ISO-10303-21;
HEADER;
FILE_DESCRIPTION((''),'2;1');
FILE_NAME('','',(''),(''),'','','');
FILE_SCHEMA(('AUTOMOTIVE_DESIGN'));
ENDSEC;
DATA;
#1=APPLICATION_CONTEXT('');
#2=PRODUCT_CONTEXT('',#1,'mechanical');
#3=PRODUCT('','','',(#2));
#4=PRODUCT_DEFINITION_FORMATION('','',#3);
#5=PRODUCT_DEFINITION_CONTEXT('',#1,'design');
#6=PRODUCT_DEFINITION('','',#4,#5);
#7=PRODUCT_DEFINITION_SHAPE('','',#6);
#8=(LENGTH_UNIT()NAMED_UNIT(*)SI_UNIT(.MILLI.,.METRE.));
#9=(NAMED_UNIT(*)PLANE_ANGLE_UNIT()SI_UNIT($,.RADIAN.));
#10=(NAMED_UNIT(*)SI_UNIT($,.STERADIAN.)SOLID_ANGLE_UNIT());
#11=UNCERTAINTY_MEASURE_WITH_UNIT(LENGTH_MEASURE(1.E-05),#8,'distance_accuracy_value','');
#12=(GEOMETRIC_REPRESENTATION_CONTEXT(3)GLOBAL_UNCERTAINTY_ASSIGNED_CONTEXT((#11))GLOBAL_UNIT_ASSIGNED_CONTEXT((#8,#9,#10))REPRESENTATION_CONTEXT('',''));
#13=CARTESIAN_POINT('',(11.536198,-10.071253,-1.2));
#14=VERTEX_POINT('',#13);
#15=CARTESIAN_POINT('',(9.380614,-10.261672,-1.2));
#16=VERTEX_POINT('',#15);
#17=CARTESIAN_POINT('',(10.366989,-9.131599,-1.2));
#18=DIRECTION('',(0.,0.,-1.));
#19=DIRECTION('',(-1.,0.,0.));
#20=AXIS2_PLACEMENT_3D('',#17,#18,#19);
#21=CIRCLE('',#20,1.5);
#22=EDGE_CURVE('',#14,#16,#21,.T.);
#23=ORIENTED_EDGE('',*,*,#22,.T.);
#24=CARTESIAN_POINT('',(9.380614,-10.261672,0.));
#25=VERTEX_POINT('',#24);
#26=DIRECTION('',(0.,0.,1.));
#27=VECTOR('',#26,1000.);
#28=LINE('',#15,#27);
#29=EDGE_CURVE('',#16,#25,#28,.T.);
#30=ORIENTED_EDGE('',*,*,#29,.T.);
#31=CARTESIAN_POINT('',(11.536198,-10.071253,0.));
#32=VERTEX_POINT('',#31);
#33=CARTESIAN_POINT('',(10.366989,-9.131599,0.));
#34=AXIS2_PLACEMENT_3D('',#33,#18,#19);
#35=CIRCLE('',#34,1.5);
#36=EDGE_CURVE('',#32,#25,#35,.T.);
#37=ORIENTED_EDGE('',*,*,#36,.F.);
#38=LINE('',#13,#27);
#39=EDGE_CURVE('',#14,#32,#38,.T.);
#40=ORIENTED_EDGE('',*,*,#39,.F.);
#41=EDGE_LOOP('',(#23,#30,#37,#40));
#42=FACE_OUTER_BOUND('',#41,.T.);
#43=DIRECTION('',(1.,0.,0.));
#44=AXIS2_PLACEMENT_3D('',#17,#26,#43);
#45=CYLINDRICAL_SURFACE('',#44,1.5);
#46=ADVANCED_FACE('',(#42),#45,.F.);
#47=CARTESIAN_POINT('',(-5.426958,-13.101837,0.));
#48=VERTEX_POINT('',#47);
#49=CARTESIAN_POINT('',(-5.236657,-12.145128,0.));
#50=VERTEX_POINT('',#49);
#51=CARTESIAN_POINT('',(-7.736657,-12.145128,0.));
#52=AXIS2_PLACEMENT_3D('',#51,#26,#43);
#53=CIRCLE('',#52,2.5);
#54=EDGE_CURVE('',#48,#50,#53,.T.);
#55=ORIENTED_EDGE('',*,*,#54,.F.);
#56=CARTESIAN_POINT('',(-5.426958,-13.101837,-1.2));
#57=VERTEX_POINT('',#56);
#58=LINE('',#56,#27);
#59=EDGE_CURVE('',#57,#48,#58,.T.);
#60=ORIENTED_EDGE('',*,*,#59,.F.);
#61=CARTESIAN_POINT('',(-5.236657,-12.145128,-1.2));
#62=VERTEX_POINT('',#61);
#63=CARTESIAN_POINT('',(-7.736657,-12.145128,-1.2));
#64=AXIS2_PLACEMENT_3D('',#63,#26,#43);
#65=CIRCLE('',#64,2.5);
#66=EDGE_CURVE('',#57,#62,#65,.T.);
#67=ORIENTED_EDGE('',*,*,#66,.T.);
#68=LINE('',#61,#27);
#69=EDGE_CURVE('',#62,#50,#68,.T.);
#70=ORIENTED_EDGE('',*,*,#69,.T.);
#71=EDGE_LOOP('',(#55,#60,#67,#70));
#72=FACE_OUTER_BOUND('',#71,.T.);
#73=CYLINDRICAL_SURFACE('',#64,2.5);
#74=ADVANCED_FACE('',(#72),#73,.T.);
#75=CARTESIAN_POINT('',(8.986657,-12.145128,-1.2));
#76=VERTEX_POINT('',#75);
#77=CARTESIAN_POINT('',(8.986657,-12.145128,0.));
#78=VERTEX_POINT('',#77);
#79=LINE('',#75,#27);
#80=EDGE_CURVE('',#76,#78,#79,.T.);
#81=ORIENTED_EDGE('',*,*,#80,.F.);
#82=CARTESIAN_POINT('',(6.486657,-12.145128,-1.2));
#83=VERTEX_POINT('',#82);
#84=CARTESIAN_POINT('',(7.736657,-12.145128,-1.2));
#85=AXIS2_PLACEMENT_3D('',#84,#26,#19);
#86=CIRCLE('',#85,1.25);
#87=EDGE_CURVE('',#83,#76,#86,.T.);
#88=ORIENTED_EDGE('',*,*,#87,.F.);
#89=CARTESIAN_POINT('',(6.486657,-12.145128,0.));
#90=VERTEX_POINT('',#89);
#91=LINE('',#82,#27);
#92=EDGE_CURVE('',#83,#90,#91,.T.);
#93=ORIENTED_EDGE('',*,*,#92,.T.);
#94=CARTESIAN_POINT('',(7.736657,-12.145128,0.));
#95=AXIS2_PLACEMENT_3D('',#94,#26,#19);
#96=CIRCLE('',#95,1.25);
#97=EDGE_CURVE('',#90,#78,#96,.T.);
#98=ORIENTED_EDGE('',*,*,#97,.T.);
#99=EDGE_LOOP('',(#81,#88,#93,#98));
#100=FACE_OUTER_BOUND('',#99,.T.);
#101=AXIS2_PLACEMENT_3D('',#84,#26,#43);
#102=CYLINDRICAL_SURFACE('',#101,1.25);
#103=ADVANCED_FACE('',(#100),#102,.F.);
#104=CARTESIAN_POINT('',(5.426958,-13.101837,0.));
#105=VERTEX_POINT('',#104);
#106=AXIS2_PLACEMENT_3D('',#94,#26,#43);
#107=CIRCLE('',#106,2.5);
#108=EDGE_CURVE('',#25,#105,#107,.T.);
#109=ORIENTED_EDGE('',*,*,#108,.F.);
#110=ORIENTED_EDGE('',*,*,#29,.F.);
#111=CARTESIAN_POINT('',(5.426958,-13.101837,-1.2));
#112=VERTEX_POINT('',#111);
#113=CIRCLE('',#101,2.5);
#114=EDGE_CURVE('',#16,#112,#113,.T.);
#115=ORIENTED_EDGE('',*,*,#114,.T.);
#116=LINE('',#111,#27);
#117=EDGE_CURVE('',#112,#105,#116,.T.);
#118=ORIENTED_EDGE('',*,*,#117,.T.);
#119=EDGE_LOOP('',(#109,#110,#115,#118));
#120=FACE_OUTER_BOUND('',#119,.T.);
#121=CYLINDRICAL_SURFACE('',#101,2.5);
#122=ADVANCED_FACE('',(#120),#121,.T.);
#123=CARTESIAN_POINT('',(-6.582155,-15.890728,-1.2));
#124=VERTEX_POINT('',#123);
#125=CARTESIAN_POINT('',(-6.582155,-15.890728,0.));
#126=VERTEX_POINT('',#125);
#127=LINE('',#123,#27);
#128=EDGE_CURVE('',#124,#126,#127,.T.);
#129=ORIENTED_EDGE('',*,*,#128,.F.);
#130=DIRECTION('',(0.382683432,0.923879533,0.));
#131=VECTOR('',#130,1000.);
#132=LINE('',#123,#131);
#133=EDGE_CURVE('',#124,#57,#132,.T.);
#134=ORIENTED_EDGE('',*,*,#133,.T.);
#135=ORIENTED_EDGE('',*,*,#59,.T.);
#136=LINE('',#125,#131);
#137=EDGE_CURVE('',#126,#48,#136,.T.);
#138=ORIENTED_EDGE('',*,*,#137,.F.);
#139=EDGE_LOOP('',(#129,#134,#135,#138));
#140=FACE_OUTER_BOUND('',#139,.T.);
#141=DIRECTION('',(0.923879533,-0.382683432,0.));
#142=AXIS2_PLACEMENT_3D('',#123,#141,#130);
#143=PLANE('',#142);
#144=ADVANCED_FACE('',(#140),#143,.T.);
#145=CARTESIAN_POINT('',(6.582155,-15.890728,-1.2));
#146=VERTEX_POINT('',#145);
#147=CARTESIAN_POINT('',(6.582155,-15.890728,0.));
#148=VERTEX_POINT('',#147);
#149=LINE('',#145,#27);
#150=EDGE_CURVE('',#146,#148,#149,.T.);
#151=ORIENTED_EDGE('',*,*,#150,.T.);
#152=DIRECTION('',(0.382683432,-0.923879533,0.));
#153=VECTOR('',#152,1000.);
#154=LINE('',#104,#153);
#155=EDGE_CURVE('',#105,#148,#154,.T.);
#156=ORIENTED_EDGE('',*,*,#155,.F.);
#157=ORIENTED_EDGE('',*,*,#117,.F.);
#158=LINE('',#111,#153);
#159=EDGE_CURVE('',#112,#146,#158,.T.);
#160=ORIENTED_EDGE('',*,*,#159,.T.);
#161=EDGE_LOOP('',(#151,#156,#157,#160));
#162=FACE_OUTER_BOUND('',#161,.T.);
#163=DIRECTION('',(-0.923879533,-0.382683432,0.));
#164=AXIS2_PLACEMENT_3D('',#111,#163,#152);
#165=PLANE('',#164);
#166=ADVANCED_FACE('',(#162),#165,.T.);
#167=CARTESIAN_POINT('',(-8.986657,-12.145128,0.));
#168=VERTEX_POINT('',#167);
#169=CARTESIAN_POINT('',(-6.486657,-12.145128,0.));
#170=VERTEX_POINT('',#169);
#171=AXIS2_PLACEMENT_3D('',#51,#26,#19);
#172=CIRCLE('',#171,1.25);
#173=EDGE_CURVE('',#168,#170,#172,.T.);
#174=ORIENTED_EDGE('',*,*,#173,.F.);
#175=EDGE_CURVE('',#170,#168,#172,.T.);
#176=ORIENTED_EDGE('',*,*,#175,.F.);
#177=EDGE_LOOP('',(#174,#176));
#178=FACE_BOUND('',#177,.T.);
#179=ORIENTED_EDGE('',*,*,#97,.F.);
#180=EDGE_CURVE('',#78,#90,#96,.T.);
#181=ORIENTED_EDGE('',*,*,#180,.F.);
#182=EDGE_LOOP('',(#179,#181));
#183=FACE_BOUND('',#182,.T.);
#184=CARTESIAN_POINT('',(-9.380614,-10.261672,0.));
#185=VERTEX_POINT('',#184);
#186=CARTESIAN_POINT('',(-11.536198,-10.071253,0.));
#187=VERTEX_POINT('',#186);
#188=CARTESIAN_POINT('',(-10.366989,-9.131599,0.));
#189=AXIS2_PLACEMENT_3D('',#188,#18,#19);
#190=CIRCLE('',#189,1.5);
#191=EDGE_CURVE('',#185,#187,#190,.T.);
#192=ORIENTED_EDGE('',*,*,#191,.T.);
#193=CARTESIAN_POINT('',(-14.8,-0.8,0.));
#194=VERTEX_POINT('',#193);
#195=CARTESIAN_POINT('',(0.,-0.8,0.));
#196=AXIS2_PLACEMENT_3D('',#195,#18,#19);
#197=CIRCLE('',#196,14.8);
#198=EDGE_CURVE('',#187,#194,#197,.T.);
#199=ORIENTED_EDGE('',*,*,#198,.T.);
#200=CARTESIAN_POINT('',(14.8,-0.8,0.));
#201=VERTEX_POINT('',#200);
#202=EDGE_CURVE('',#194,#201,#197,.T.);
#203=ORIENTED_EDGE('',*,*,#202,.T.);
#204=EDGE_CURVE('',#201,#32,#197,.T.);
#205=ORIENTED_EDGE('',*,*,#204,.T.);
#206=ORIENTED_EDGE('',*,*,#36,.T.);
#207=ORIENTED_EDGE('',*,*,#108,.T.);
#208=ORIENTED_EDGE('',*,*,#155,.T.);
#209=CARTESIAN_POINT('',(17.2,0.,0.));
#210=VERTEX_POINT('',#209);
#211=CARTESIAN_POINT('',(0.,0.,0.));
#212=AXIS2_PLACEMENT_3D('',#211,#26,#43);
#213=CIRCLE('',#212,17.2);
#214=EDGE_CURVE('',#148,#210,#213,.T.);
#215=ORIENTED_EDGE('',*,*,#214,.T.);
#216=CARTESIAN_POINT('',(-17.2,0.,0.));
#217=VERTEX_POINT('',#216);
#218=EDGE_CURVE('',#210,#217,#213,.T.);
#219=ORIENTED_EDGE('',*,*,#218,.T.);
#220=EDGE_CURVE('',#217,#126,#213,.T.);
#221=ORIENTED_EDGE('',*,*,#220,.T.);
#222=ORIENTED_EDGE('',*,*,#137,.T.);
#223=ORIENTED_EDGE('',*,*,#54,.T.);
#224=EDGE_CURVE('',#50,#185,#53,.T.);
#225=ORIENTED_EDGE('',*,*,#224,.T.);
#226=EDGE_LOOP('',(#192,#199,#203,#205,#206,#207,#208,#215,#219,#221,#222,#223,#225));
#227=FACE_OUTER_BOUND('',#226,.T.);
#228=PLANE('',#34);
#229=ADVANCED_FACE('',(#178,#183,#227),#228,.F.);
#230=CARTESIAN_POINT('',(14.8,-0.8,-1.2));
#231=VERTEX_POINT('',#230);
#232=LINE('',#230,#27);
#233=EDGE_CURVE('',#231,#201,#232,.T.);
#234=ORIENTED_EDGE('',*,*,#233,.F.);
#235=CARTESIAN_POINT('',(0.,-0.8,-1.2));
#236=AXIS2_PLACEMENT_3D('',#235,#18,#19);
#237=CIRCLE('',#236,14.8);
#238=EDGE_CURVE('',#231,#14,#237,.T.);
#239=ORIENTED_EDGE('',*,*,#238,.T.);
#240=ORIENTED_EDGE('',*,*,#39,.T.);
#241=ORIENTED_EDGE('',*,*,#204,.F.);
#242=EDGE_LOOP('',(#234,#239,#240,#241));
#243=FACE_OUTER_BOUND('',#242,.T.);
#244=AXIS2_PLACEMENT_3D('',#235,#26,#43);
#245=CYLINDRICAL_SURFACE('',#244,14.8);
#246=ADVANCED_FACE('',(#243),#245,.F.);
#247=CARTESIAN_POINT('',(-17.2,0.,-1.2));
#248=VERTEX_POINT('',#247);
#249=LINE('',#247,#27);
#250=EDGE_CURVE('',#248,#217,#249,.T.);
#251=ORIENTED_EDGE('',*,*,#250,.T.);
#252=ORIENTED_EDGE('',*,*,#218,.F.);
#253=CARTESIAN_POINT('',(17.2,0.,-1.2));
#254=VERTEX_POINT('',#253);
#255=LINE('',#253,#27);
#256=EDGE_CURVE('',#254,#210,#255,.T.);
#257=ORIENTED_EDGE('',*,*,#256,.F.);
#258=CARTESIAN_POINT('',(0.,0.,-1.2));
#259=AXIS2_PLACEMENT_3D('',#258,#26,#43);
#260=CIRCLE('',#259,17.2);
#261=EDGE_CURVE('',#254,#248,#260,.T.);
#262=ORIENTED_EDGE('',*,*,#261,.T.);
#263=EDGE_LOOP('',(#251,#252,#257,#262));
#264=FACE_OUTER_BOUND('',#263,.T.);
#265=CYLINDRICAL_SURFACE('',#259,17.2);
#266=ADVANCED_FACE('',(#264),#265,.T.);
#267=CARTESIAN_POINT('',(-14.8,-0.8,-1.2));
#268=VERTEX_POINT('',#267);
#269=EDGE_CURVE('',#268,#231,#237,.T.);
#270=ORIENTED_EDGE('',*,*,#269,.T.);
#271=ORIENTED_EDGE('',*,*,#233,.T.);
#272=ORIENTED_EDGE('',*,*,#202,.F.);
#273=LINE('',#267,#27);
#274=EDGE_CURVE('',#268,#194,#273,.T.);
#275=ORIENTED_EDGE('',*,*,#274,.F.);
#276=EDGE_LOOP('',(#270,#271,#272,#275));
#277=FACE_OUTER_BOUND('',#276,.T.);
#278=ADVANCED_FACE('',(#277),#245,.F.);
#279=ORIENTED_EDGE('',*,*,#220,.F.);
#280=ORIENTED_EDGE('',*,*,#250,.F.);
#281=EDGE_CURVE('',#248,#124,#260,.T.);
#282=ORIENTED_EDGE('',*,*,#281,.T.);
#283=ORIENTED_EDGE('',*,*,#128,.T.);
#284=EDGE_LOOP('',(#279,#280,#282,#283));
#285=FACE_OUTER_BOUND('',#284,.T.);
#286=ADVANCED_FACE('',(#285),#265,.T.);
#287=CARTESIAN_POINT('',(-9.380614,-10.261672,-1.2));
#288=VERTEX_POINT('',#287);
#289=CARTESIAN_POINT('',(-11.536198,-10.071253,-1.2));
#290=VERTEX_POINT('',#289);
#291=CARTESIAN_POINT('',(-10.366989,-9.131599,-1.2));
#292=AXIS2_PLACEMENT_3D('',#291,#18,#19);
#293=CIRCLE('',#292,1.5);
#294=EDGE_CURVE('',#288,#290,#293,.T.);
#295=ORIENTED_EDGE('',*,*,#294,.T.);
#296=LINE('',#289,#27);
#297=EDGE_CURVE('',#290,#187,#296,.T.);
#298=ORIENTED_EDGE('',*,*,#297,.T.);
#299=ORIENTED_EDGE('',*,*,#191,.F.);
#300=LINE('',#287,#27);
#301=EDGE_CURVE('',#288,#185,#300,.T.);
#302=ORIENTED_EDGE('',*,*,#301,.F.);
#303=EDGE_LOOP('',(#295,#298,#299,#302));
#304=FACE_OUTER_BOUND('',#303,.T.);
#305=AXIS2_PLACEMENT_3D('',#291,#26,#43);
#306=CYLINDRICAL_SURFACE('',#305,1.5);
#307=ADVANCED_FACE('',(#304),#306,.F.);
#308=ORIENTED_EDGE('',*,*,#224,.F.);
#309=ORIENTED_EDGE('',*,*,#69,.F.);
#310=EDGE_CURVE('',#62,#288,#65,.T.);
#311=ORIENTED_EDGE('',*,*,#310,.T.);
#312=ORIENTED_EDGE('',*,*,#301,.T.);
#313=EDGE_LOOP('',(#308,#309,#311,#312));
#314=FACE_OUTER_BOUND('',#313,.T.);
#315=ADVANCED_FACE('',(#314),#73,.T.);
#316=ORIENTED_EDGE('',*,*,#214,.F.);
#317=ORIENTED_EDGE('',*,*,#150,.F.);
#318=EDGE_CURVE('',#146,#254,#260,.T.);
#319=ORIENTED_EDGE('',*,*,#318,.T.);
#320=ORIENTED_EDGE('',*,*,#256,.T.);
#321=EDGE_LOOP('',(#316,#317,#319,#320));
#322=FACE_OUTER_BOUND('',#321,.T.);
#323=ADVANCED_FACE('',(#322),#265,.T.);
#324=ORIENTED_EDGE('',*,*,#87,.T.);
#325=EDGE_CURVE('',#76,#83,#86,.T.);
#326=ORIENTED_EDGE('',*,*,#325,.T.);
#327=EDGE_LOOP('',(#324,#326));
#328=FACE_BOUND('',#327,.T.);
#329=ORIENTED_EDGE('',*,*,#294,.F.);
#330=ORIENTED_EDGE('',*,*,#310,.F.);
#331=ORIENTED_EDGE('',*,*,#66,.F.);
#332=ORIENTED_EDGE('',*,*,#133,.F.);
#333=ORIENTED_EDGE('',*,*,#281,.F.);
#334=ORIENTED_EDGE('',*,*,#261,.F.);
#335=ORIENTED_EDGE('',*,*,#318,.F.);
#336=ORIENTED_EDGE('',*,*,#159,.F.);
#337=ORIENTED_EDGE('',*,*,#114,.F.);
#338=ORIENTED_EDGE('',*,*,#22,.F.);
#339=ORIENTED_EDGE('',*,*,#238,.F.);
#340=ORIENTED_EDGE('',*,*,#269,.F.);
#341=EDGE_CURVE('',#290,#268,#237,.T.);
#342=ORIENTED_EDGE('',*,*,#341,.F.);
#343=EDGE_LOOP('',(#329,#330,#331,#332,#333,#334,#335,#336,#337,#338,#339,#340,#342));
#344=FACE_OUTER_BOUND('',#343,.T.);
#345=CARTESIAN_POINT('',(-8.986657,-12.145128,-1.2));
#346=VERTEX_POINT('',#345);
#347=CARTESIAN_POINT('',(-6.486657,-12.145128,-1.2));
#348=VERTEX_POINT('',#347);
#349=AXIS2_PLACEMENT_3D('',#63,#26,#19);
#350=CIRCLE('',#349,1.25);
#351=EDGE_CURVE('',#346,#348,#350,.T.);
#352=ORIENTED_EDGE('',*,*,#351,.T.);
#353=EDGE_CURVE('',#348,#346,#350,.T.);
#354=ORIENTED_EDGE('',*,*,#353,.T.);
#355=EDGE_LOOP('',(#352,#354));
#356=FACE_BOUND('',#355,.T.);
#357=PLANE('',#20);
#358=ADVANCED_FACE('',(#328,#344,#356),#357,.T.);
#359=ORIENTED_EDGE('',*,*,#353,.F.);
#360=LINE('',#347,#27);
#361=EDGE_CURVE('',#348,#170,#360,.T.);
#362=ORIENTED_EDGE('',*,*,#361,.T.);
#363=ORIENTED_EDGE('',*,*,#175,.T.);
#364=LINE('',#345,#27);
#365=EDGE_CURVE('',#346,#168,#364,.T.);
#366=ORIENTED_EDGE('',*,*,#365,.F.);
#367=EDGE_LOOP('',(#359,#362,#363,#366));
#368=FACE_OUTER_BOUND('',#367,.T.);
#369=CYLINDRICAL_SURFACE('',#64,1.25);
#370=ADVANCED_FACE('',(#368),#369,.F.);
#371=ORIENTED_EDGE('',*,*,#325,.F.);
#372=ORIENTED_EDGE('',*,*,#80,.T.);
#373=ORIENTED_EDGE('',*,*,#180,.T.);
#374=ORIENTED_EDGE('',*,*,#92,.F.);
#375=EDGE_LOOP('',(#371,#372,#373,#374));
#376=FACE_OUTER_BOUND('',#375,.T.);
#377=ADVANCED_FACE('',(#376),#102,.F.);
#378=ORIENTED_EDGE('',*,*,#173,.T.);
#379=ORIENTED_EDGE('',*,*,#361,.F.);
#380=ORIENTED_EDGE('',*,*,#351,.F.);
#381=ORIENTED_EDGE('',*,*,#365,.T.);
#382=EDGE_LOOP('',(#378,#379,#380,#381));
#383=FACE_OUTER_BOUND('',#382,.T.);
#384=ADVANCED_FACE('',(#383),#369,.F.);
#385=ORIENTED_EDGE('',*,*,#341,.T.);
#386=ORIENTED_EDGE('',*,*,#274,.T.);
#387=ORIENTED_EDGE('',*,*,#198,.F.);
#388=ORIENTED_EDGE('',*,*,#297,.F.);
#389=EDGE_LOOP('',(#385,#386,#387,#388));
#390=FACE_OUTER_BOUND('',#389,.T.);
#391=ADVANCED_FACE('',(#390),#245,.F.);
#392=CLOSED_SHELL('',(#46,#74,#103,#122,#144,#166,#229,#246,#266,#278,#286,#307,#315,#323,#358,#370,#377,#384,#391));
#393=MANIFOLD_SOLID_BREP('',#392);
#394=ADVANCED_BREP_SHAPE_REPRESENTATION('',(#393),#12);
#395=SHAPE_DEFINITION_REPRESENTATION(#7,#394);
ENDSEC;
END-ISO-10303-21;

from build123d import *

# Parameters (mm, degrees)
SKETCH_1_R      = 1.25
EXTRUDE_1_DEPTH = 1.2


with BuildPart() as part:
    # 草图1 → 凸台-拉伸1 (new body)
    with BuildSketch(Plane.XY):
        with BuildLine():
            Line((5.426958413, -13.101836603), (6.582155037, -15.890727959))
            ThreePointArc((6.582155037, -15.890727959), (0, 17.2), (-6.582155037, -15.890727959))
            Line((-6.582155037, -15.890727959), (-5.426958413, -13.101836603))
            ThreePointArc((-5.426958413, -13.101836603), (-6.278083953, -10.114718223), (-9.380614428, -10.261672481))
            ThreePointArc((-9.380614428, -10.261672481), (-10.498981278, -10.625780527), (-11.536197995, -10.071253196))
            ThreePointArc((-11.536197995, -10.071253196), (0, 14), (11.536197995, -10.071253196))
            ThreePointArc((11.536197995, -10.071253196), (10.498981278, -10.625780527), (9.380614428, -10.261672481))
            ThreePointArc((9.380614428, -10.261672481), (6.278083953, -10.114718223), (5.426958413, -13.101836603))
        make_face()
        with Locations(Location((-7.736657244, -12.145128022, 0), (0, 0, 180))):
            Circle(SKETCH_1_R, mode=Mode.SUBTRACT)
        with Locations(Location((7.736657244, -12.145128022, 0), (0, 0, 180))):
            Circle(SKETCH_1_R, mode=Mode.SUBTRACT)
    extrude(amount=-EXTRUDE_1_DEPTH)


solid = part.part
